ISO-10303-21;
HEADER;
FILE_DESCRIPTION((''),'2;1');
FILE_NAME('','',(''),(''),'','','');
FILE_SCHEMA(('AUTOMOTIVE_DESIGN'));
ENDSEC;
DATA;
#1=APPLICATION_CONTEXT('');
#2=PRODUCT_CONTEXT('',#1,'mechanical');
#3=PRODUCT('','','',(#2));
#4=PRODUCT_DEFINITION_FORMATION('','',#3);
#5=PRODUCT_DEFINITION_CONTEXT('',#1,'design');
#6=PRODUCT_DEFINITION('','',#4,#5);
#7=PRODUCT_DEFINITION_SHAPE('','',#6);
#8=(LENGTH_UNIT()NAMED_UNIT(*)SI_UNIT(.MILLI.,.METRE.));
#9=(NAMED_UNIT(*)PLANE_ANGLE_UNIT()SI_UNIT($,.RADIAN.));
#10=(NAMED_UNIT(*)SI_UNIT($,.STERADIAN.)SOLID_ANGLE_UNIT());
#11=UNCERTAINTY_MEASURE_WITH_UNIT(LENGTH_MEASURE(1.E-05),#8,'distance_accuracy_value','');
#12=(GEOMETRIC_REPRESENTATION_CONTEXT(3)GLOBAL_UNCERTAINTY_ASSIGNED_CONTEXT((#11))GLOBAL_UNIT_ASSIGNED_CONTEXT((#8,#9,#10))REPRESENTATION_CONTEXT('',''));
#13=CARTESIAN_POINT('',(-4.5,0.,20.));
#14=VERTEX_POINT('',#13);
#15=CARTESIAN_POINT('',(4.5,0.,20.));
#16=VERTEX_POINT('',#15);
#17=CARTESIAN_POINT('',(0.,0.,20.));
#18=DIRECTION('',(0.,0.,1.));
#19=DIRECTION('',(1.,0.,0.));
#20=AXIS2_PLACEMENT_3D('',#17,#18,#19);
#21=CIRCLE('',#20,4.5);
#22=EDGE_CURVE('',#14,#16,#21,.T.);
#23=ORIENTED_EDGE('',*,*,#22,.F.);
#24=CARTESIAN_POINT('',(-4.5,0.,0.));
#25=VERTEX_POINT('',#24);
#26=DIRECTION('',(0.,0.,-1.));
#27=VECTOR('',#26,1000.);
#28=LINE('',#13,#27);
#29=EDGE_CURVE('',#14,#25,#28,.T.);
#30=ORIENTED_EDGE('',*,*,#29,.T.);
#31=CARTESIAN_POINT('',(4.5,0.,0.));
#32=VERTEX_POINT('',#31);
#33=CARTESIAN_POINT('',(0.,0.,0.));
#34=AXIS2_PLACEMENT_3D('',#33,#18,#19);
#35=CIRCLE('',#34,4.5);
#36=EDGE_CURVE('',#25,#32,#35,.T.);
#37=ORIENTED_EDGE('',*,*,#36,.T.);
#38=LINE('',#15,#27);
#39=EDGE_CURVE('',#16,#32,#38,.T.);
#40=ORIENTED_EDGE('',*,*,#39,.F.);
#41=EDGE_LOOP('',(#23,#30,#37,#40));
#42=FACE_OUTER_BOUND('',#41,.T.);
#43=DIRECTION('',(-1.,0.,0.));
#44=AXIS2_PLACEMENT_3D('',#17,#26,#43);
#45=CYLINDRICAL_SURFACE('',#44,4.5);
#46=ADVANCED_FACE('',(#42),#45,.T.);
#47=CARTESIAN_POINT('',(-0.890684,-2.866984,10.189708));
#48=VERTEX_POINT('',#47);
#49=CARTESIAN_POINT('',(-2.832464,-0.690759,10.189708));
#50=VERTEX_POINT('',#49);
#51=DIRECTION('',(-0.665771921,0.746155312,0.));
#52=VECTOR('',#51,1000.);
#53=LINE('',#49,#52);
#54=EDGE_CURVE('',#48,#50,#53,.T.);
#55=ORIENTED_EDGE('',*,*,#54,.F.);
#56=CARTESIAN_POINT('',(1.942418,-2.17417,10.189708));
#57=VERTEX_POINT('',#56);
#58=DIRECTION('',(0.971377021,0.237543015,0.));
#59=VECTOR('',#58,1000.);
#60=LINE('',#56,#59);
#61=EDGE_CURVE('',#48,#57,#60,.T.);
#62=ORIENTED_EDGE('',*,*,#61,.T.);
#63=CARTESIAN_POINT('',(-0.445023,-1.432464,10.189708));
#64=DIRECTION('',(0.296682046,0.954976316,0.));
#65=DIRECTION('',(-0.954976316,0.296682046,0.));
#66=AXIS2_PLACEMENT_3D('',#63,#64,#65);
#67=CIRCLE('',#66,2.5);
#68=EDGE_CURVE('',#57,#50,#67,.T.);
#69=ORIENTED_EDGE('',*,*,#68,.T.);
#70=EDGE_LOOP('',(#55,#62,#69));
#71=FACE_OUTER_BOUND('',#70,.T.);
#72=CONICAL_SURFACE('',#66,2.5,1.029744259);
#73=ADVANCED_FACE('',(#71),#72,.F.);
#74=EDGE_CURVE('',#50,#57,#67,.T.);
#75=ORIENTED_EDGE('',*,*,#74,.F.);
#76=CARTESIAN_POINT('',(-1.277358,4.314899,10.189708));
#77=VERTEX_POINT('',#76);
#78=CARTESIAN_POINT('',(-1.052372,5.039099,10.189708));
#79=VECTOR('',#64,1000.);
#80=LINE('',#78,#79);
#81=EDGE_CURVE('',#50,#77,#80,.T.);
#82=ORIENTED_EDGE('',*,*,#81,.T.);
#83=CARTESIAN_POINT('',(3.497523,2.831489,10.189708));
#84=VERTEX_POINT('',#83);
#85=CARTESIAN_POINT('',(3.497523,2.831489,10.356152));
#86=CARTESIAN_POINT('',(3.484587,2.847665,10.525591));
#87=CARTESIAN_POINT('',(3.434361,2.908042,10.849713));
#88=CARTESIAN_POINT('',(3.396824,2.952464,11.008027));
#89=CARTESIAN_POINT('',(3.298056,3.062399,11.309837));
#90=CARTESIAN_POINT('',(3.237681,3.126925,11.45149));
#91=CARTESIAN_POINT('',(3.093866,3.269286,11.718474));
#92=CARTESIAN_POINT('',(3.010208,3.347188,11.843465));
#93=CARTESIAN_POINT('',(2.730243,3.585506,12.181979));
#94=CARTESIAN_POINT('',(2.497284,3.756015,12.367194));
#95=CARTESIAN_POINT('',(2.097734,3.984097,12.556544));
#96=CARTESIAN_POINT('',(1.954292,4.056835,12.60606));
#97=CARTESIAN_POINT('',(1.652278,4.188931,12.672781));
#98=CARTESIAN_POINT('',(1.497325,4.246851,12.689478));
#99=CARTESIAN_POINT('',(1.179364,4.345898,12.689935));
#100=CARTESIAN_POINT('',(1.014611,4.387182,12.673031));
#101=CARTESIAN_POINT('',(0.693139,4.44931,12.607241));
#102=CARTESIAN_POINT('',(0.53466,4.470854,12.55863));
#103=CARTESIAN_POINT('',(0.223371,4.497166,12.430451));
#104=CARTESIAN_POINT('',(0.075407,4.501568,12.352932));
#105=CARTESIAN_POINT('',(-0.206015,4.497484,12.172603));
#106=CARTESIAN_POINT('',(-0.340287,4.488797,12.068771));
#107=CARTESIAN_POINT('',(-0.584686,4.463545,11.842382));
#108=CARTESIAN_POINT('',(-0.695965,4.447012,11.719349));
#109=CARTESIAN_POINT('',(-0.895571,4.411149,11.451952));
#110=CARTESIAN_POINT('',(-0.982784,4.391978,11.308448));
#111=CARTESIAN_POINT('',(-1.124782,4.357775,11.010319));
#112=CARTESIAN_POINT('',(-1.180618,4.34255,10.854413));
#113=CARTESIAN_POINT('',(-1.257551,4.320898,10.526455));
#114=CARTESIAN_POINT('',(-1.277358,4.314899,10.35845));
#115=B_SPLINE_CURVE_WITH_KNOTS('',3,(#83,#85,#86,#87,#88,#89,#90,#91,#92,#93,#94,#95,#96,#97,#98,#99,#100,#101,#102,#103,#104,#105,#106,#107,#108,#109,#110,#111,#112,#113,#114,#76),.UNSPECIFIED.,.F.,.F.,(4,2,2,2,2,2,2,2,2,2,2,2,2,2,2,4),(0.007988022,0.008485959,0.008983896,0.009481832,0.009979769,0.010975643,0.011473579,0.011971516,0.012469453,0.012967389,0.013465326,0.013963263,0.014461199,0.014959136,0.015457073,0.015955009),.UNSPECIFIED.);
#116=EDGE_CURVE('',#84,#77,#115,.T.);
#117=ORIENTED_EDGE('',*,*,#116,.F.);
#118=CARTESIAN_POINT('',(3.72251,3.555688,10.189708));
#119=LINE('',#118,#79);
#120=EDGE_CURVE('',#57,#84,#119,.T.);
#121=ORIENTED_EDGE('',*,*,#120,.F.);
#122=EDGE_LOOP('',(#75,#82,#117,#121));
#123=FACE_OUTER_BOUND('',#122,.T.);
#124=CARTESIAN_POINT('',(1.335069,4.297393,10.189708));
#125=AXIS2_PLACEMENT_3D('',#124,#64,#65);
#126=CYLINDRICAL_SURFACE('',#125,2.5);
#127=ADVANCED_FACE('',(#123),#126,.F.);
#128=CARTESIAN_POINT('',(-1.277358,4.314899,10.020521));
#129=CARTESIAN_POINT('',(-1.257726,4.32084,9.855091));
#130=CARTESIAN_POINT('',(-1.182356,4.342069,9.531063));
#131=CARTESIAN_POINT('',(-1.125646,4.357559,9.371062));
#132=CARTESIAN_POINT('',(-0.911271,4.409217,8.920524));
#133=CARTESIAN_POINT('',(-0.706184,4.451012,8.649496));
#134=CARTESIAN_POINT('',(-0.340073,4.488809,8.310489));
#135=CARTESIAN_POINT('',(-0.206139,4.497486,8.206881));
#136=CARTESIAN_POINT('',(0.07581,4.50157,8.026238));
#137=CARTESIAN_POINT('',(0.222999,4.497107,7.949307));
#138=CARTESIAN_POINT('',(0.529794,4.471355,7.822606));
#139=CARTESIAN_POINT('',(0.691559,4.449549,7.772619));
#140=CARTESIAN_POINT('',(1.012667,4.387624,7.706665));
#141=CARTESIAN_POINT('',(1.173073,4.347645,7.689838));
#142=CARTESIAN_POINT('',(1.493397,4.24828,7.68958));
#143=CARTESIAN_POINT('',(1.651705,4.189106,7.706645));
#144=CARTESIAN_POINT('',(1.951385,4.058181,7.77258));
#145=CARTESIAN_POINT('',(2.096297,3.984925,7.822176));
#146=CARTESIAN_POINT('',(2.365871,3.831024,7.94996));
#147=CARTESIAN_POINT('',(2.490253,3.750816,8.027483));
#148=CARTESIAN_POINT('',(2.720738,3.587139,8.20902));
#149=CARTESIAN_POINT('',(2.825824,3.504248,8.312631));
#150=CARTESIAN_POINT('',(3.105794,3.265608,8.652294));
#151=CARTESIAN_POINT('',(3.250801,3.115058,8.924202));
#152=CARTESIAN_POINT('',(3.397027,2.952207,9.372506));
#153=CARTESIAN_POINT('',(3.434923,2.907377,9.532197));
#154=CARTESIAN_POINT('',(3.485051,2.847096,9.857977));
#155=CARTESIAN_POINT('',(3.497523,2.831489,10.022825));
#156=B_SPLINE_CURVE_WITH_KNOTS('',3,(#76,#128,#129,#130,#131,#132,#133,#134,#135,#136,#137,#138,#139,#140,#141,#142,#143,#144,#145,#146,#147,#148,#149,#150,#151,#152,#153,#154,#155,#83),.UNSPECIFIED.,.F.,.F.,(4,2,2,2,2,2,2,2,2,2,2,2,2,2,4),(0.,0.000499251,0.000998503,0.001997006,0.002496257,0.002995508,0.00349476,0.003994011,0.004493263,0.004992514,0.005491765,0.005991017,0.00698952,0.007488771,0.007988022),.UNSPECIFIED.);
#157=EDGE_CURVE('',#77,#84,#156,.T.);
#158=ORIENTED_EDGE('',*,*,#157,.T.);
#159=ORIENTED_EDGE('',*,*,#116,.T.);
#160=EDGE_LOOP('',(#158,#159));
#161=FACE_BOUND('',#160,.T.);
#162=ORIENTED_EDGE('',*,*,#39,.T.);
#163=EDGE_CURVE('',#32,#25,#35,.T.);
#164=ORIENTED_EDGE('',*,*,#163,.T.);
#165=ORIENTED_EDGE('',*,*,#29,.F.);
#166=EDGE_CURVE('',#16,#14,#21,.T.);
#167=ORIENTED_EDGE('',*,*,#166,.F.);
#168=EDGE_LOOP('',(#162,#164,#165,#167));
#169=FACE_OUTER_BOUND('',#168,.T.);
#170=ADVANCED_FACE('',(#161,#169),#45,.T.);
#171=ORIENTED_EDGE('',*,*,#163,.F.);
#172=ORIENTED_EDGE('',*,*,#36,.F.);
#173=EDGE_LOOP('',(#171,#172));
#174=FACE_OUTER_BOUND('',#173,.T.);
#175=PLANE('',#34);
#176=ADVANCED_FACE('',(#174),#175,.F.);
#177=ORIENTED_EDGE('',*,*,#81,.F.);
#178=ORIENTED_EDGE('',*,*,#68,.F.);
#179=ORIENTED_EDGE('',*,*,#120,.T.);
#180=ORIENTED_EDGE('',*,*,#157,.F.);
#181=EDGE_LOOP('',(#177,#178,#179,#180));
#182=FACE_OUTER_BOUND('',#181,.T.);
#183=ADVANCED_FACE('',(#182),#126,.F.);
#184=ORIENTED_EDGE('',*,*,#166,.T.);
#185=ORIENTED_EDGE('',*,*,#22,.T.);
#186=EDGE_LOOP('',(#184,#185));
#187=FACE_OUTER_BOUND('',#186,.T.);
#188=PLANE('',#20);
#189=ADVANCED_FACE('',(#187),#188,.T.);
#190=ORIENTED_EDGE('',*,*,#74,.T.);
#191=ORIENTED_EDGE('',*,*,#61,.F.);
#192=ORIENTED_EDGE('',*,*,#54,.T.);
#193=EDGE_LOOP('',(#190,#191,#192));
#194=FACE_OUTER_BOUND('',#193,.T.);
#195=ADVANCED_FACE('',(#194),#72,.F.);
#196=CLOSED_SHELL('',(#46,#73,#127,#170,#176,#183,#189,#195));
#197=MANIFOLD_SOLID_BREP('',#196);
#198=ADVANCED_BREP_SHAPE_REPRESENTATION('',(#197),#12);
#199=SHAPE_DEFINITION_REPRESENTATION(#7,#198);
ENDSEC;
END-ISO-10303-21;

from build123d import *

# Parameters (mm, degrees)
SKETCH_1_R             = 4.5
EXTRUDE_1_DEPTH        = 20
HOLE_WIZARD_M6_1_D     = 5
HOLE_WIZARD_M6_1_DEPTH = 6
HOLE_WIZARD_M6_1_TIP   = 1.502151548


with BuildPart() as part:
    # 草图1 → 凸台-拉伸1 (new body)
    with BuildSketch(Plane.XY):
        Circle(SKETCH_1_R)
    extrude(amount=EXTRUDE_1_DEPTH)

    # M6 螺纹孔1
    with Locations(Plane(origin=(1.335069206, 4.297393421, 10.189708397), x_dir=(0.95497631577, -0.296682045829, 0), z_dir=(0.296682045829, 0.95497631577, 0))):
        with Locations((0, 0)):
            Hole(HOLE_WIZARD_M6_1_D / 2, depth=HOLE_WIZARD_M6_1_DEPTH)
            with Locations((0, 0, -(HOLE_WIZARD_M6_1_DEPTH + HOLE_WIZARD_M6_1_TIP / 2))):  # 118° drill point
                Cone(0, HOLE_WIZARD_M6_1_D / 2, HOLE_WIZARD_M6_1_TIP, mode=Mode.SUBTRACT)


solid = part.part
